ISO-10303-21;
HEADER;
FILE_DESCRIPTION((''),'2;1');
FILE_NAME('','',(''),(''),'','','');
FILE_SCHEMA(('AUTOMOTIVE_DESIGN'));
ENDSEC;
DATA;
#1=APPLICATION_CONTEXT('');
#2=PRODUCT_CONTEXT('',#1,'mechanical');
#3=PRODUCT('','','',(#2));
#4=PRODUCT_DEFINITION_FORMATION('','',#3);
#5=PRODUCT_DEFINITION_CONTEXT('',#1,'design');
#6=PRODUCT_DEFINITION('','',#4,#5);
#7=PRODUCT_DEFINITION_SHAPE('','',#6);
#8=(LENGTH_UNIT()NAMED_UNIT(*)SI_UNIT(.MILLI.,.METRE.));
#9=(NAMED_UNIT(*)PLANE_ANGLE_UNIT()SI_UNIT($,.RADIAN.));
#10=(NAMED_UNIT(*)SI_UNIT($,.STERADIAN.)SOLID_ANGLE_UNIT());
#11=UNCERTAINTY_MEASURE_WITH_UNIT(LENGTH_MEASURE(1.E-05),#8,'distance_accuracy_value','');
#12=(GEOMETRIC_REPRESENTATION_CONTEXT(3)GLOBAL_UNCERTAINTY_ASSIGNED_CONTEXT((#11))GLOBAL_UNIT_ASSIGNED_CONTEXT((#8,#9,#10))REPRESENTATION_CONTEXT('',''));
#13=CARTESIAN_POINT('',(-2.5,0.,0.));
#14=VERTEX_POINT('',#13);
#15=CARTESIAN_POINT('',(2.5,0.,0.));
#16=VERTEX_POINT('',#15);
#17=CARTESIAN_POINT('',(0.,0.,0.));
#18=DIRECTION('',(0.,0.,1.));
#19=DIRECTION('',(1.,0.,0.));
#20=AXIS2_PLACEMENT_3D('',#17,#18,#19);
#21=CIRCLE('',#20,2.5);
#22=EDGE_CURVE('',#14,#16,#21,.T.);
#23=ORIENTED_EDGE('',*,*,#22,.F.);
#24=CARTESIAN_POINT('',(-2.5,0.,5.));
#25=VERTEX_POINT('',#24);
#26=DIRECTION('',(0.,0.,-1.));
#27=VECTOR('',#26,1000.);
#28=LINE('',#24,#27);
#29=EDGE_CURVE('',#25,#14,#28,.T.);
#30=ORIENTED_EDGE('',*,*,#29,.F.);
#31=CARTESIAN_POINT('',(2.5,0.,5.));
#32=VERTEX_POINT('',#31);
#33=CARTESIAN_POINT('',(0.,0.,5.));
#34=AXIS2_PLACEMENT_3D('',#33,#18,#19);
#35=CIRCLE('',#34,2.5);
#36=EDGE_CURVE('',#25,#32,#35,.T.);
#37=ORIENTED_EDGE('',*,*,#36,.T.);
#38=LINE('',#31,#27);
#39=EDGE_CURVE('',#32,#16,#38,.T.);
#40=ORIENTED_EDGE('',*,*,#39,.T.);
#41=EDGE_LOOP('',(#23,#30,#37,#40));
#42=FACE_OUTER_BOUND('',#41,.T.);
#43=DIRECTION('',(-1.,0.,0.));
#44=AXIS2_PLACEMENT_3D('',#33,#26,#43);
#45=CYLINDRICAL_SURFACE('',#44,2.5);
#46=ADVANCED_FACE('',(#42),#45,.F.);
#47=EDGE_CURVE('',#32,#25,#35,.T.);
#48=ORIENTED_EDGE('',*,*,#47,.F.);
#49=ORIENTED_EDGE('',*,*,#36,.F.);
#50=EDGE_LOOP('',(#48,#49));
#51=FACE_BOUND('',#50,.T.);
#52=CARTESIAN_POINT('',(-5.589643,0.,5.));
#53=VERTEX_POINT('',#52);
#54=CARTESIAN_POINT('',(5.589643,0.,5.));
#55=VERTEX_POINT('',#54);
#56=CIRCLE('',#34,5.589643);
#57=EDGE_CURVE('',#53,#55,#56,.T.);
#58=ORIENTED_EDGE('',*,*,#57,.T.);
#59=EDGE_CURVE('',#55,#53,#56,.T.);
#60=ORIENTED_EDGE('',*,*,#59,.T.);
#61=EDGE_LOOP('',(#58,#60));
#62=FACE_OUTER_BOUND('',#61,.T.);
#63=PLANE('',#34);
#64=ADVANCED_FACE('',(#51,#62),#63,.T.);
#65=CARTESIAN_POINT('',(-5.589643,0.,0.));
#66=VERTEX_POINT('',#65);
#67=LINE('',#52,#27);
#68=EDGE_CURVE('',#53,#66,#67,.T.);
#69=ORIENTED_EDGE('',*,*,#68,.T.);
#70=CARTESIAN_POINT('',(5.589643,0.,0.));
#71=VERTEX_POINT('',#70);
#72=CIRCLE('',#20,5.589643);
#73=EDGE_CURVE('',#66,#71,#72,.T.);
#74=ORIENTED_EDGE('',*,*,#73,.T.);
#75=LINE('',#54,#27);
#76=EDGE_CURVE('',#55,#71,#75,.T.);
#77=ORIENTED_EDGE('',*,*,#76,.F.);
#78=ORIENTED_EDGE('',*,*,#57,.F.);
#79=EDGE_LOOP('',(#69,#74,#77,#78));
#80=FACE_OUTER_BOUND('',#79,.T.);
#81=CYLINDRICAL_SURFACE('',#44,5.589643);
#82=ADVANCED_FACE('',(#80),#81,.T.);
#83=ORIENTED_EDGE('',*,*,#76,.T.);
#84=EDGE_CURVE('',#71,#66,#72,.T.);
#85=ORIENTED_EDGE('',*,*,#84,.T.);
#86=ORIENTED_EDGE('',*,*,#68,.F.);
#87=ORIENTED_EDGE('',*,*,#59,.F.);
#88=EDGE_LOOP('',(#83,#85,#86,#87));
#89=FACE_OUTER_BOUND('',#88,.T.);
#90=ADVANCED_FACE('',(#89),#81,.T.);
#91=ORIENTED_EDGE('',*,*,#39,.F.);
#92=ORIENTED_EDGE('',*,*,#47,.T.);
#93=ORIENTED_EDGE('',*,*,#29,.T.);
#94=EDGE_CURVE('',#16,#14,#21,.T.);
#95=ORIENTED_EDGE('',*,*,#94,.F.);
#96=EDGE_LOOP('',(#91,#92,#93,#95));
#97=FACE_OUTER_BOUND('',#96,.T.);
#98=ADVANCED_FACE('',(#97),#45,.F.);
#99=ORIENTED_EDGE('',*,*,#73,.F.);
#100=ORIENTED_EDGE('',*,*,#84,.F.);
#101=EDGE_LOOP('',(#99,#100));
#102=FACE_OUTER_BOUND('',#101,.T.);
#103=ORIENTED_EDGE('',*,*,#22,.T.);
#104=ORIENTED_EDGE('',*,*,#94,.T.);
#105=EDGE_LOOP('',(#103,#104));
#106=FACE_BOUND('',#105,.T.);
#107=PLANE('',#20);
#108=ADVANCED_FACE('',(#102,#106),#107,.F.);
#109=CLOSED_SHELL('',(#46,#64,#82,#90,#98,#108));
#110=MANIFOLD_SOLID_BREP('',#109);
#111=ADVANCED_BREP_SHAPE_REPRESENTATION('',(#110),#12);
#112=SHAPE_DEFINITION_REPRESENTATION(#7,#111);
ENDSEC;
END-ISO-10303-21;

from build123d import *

# Parameters (mm, degrees)
SKETCH1_R           = 5.589643184
SKETCH1_R_2         = 2.5
BOSS_EXTRUDE1_DEPTH = 5


with BuildPart() as part:
    # Sketch1 → Boss-Extrude1 (new body)
    with BuildSketch(Plane.XY):
        Circle(SKETCH1_R)
        Circle(SKETCH1_R_2, mode=Mode.SUBTRACT)
    extrude(amount=BOSS_EXTRUDE1_DEPTH)


solid = part.part
